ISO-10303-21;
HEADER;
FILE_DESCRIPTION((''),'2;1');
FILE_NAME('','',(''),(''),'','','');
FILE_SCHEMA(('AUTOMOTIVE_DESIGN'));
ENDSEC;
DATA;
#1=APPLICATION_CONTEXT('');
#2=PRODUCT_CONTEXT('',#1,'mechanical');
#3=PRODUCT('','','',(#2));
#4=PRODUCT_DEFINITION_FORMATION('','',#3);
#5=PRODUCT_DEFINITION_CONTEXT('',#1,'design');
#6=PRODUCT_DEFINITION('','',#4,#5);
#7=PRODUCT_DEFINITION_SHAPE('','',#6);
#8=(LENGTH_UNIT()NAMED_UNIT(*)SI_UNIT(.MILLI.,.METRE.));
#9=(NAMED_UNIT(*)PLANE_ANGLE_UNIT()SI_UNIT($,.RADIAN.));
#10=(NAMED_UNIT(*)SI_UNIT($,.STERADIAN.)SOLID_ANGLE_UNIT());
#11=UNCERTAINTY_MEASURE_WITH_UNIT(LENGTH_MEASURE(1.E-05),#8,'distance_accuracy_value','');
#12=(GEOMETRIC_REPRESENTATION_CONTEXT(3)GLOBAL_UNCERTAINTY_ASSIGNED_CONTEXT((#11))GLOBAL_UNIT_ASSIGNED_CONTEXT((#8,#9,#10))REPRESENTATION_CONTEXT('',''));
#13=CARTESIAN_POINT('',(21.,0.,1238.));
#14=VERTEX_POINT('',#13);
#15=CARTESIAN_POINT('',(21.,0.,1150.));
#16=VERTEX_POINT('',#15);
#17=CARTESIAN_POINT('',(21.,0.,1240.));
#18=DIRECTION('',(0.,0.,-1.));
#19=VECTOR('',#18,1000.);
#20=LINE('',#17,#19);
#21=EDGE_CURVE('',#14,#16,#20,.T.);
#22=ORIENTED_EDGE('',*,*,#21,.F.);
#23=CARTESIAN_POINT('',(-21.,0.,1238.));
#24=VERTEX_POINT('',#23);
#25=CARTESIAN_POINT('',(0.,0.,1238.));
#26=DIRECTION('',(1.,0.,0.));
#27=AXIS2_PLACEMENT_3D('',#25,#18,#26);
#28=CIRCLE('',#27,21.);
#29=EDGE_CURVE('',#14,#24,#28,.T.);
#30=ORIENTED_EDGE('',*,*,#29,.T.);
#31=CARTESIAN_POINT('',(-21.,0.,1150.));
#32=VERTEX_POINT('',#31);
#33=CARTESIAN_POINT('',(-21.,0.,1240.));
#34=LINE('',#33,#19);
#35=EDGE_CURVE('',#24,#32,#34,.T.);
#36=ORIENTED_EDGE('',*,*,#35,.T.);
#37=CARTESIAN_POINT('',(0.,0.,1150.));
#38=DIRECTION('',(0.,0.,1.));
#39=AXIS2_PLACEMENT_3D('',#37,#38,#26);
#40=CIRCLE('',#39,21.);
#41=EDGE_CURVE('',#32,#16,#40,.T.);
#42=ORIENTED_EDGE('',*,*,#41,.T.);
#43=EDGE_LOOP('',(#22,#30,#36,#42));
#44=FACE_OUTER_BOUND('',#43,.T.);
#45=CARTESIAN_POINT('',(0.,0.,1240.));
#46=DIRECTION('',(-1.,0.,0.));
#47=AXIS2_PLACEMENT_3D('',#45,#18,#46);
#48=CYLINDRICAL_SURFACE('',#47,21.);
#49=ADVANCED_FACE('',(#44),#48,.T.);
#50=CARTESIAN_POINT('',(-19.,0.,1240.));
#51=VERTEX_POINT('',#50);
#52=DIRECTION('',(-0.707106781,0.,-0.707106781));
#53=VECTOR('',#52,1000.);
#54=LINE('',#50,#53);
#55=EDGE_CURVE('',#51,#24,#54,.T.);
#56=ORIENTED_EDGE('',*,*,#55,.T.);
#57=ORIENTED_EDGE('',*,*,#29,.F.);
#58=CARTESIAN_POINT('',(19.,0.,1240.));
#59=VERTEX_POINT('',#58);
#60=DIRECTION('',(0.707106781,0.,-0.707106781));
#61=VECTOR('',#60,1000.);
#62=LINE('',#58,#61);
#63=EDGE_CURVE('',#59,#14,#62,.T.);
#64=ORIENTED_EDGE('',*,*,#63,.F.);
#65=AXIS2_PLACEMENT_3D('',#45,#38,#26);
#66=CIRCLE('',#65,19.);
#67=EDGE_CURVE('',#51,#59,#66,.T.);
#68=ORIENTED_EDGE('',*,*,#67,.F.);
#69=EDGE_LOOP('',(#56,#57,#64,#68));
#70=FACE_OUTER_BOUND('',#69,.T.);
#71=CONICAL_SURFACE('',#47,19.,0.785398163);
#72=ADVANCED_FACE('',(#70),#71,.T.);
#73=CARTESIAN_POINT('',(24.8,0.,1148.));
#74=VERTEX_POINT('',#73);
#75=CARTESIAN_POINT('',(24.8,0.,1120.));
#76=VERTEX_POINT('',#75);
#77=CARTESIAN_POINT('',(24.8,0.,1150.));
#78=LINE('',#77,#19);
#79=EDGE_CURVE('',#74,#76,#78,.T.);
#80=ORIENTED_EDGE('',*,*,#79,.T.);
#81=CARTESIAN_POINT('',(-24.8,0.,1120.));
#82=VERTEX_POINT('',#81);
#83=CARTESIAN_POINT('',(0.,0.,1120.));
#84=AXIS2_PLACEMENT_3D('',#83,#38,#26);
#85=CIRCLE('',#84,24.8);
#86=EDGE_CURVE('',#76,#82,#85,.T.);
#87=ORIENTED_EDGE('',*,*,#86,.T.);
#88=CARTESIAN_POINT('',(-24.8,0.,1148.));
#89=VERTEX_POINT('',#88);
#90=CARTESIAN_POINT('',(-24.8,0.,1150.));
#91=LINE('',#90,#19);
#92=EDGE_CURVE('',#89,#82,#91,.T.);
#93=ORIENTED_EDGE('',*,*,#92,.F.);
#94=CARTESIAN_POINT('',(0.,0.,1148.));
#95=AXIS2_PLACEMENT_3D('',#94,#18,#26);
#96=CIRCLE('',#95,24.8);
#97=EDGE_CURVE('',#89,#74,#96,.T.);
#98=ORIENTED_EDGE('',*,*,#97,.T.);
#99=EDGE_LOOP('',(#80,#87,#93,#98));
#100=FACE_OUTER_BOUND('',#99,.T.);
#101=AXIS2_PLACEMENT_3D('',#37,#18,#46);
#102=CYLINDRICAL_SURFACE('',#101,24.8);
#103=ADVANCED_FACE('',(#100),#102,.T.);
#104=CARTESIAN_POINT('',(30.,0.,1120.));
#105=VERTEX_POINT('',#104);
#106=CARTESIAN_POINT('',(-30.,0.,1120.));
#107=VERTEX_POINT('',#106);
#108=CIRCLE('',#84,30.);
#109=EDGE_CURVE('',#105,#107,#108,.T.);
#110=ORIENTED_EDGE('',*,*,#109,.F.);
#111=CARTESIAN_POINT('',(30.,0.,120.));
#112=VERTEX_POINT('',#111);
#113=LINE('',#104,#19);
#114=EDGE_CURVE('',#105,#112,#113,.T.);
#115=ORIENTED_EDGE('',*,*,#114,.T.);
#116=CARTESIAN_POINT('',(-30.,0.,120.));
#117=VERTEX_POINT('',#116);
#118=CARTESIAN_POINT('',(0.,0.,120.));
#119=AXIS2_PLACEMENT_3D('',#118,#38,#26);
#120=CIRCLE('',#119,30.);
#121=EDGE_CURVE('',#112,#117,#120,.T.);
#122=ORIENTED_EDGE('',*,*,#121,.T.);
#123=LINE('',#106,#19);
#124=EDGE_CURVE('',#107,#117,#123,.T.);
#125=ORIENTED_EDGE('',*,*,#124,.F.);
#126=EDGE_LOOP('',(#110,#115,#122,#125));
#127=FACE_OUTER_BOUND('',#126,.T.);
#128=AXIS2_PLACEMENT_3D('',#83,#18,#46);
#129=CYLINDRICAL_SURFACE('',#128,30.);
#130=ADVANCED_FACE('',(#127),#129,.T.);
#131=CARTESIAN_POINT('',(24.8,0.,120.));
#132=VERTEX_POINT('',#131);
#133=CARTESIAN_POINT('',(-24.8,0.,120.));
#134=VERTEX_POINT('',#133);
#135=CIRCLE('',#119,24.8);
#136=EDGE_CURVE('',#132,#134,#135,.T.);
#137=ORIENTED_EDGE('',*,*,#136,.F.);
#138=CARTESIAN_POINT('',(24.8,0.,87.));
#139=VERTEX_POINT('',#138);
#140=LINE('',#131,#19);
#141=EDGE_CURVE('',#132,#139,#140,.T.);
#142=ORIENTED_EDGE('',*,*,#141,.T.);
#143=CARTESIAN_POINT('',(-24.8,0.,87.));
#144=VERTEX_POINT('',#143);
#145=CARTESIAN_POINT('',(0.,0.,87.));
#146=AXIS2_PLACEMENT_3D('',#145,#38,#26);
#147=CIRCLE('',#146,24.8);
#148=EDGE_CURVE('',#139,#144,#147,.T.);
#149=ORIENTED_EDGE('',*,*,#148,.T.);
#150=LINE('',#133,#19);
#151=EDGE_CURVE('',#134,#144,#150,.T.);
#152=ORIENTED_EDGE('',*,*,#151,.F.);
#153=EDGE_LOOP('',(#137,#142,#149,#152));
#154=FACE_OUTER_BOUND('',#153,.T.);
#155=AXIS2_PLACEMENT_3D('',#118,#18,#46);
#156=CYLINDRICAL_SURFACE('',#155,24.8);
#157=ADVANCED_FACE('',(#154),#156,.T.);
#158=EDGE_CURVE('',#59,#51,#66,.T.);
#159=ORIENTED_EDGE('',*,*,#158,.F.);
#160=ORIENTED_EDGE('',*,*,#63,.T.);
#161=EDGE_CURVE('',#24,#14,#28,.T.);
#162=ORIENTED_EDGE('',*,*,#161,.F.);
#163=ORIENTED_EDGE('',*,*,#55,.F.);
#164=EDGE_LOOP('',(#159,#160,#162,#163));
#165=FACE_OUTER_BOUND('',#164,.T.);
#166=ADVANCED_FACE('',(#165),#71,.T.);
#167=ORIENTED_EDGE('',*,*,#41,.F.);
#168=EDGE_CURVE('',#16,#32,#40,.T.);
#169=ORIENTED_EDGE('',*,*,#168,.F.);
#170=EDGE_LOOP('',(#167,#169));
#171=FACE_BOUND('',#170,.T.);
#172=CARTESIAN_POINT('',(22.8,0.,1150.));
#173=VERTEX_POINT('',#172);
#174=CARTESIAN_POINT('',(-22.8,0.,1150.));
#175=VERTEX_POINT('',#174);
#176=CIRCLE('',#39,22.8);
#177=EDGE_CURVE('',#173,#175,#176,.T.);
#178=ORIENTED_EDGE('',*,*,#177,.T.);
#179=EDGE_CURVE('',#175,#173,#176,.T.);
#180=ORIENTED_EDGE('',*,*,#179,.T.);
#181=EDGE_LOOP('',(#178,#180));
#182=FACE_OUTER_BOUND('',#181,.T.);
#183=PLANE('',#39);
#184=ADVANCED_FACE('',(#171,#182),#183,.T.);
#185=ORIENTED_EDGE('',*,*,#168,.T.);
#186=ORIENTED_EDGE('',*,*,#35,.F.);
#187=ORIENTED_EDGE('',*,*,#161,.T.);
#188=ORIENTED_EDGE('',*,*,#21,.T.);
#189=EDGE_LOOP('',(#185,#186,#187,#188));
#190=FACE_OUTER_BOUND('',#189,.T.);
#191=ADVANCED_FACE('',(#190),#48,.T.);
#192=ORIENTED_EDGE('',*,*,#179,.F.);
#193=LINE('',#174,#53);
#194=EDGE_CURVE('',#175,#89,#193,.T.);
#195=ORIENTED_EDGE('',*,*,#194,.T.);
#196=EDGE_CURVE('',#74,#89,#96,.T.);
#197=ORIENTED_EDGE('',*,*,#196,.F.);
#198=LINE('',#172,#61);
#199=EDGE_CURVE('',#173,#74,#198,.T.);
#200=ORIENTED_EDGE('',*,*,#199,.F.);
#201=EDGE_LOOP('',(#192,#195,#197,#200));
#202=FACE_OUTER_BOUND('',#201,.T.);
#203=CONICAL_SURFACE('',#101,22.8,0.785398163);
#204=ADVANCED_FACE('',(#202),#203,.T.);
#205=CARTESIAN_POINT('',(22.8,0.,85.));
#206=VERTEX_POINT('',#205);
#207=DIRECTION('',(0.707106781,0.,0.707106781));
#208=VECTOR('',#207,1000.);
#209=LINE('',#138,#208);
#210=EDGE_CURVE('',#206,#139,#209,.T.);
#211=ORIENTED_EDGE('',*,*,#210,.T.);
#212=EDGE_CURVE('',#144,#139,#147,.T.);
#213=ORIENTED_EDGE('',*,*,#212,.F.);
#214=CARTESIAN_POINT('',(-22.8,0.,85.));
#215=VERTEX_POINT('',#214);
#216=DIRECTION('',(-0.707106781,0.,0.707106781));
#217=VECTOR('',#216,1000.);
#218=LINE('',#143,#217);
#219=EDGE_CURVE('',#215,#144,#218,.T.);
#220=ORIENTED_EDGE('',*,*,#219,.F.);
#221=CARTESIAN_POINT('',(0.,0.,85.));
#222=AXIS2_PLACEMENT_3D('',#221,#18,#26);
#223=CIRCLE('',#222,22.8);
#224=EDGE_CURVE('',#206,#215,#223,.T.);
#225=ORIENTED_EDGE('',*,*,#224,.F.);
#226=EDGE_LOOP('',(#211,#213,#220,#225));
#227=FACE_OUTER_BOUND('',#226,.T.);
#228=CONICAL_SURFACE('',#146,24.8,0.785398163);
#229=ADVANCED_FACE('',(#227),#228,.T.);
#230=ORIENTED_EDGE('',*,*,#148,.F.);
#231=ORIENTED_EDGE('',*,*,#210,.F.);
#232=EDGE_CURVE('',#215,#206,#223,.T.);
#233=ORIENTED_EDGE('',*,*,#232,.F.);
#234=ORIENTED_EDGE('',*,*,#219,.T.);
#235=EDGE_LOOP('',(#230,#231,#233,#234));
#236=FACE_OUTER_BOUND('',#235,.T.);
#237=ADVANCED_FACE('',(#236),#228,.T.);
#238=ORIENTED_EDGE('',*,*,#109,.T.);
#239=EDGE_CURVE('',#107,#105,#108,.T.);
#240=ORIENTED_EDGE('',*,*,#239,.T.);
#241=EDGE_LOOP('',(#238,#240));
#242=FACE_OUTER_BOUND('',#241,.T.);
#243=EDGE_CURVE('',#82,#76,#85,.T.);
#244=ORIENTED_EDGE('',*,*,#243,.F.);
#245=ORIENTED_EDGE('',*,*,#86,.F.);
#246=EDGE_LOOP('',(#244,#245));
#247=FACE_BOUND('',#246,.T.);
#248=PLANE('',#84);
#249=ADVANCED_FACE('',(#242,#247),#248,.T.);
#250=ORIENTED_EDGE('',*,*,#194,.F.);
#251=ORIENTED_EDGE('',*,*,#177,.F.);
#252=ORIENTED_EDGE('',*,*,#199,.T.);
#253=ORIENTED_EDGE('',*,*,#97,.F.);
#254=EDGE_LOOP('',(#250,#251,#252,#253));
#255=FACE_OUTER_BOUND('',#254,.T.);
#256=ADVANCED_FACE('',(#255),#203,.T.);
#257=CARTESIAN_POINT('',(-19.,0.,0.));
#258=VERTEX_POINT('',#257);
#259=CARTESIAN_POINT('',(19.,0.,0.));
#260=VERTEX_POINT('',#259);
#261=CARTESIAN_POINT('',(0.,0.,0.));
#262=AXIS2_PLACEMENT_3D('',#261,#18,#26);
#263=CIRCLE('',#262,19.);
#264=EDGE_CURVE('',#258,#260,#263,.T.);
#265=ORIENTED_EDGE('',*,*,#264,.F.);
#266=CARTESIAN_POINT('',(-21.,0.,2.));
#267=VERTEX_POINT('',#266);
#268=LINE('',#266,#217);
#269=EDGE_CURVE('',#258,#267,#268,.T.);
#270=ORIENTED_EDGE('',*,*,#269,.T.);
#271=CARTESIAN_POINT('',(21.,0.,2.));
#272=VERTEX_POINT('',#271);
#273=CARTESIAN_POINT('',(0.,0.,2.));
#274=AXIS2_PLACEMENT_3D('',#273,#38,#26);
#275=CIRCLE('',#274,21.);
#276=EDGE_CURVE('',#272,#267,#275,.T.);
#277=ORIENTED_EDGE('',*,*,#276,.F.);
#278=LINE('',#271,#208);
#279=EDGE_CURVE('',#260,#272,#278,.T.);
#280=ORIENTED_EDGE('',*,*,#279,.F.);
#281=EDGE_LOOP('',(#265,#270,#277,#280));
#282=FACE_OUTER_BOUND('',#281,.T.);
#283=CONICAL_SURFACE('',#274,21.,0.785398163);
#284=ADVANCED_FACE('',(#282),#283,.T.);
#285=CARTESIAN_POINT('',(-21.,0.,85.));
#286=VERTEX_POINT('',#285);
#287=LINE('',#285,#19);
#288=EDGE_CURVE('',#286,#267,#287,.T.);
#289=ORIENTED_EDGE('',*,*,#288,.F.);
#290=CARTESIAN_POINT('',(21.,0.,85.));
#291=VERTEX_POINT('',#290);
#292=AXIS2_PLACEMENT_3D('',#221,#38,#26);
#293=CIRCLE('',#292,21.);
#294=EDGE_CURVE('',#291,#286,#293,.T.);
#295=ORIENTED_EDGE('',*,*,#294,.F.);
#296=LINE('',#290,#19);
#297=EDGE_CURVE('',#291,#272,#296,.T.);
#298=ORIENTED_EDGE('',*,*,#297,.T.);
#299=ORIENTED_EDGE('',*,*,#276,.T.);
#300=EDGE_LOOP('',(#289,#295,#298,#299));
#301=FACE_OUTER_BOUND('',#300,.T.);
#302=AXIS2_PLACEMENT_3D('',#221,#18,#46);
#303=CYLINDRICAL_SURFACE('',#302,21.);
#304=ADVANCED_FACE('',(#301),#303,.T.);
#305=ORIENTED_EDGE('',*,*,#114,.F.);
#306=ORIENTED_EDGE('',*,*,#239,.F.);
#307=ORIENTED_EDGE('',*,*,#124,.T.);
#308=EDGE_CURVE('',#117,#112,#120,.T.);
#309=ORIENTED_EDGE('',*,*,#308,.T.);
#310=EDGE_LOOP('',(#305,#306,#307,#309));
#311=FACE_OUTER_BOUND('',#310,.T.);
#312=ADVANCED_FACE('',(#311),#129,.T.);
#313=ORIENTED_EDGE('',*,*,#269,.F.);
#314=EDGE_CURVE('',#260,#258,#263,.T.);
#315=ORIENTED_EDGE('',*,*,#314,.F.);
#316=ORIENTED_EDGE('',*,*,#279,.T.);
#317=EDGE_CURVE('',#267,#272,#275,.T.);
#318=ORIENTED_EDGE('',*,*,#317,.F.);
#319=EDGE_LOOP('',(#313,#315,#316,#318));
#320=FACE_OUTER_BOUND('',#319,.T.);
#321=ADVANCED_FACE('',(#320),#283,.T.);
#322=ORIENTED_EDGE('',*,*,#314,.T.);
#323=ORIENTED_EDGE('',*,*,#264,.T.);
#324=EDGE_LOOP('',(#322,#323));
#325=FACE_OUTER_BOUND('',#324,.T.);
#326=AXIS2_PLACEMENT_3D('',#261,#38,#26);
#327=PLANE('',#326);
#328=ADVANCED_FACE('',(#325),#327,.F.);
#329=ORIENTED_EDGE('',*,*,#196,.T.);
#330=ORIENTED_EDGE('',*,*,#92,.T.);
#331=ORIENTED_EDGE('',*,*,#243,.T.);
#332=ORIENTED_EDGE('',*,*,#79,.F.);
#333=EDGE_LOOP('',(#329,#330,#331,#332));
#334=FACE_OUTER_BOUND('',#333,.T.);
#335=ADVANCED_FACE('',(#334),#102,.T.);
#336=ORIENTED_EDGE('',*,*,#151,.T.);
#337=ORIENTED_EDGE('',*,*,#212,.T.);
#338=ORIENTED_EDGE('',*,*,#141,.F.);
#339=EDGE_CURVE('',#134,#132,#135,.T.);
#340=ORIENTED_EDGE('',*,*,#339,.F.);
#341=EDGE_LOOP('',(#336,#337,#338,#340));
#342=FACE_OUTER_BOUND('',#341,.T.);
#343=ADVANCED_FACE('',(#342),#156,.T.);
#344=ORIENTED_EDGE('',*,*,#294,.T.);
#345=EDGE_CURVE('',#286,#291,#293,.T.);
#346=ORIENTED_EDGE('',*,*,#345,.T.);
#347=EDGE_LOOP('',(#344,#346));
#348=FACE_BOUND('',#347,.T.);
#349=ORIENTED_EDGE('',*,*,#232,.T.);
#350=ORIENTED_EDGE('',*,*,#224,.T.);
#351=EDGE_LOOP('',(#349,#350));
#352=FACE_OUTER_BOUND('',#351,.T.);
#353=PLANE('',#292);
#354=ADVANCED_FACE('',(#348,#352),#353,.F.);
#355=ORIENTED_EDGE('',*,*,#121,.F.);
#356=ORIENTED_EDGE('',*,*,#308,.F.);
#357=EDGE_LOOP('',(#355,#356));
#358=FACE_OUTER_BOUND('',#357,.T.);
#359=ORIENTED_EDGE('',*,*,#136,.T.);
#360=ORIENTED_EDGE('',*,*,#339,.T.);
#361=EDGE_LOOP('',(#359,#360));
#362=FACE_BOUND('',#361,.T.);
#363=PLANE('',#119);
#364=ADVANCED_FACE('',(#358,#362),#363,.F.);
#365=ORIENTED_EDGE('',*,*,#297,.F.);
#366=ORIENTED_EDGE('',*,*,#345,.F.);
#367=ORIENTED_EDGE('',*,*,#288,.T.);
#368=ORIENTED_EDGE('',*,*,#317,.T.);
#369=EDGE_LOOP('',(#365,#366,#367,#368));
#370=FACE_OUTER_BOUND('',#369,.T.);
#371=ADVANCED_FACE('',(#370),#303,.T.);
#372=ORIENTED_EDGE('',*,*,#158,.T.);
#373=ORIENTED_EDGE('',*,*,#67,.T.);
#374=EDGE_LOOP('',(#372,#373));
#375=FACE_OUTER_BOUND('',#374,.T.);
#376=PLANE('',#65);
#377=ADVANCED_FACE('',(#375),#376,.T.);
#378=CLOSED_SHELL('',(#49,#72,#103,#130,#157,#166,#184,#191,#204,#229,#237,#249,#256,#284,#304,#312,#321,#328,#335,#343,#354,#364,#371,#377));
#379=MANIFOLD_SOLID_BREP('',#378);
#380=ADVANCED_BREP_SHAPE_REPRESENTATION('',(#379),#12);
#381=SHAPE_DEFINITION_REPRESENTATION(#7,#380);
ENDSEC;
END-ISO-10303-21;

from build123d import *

# Parameters (mm, degrees)
SKETCH1_R           = 21
BOSS_EXTRUDE1_DEPTH = 85
SKETCH2_R           = 24.8
BOSS_EXTRUDE2_DEPTH = 35
SKETCH3_R           = 30
BOSS_EXTRUDE3_DEPTH = 1000
SKETCH4_R           = 24.8
BOSS_EXTRUDE4_DEPTH = 30
SKETCH5_R           = 21
BOSS_EXTRUDE5_DEPTH = 90
CHAMFER2_SIZE       = 2


with BuildPart() as part:
    # Sketch1 → Boss-Extrude1 (new body)
    with BuildSketch(Plane.XY):
        Circle(SKETCH1_R)
    extrude(amount=BOSS_EXTRUDE1_DEPTH)

    # Sketch2 → Boss-Extrude2 (add)
    with BuildSketch(Plane.XY.offset(85)):
        Circle(SKETCH2_R)
    extrude(amount=BOSS_EXTRUDE2_DEPTH)

    # Sketch3 → Boss-Extrude3 (add)
    with BuildSketch(Plane.XY.offset(120)):
        Circle(SKETCH3_R)
    extrude(amount=BOSS_EXTRUDE3_DEPTH)

    # Sketch4 → Boss-Extrude4 (add)
    with BuildSketch(Plane.XY.offset(1120)):
        Circle(SKETCH4_R)
    extrude(amount=BOSS_EXTRUDE4_DEPTH)

    # Sketch5 → Boss-Extrude5 (add)
    with BuildSketch(Plane.XY.offset(1150)):
        Circle(SKETCH5_R)
    extrude(amount=BOSS_EXTRUDE5_DEPTH)

    # Chamfer2
    chamfer2_edges = [part.edges().sort_by_distance(p)[0] for p in [
        (-24.8, 0, 1150),
        (-21, 0, 1240),
        (-21, 0, 0),
        (-24.8, 0, 85),
    ]]
    chamfer(chamfer2_edges, length=CHAMFER2_SIZE)


solid = part.part
